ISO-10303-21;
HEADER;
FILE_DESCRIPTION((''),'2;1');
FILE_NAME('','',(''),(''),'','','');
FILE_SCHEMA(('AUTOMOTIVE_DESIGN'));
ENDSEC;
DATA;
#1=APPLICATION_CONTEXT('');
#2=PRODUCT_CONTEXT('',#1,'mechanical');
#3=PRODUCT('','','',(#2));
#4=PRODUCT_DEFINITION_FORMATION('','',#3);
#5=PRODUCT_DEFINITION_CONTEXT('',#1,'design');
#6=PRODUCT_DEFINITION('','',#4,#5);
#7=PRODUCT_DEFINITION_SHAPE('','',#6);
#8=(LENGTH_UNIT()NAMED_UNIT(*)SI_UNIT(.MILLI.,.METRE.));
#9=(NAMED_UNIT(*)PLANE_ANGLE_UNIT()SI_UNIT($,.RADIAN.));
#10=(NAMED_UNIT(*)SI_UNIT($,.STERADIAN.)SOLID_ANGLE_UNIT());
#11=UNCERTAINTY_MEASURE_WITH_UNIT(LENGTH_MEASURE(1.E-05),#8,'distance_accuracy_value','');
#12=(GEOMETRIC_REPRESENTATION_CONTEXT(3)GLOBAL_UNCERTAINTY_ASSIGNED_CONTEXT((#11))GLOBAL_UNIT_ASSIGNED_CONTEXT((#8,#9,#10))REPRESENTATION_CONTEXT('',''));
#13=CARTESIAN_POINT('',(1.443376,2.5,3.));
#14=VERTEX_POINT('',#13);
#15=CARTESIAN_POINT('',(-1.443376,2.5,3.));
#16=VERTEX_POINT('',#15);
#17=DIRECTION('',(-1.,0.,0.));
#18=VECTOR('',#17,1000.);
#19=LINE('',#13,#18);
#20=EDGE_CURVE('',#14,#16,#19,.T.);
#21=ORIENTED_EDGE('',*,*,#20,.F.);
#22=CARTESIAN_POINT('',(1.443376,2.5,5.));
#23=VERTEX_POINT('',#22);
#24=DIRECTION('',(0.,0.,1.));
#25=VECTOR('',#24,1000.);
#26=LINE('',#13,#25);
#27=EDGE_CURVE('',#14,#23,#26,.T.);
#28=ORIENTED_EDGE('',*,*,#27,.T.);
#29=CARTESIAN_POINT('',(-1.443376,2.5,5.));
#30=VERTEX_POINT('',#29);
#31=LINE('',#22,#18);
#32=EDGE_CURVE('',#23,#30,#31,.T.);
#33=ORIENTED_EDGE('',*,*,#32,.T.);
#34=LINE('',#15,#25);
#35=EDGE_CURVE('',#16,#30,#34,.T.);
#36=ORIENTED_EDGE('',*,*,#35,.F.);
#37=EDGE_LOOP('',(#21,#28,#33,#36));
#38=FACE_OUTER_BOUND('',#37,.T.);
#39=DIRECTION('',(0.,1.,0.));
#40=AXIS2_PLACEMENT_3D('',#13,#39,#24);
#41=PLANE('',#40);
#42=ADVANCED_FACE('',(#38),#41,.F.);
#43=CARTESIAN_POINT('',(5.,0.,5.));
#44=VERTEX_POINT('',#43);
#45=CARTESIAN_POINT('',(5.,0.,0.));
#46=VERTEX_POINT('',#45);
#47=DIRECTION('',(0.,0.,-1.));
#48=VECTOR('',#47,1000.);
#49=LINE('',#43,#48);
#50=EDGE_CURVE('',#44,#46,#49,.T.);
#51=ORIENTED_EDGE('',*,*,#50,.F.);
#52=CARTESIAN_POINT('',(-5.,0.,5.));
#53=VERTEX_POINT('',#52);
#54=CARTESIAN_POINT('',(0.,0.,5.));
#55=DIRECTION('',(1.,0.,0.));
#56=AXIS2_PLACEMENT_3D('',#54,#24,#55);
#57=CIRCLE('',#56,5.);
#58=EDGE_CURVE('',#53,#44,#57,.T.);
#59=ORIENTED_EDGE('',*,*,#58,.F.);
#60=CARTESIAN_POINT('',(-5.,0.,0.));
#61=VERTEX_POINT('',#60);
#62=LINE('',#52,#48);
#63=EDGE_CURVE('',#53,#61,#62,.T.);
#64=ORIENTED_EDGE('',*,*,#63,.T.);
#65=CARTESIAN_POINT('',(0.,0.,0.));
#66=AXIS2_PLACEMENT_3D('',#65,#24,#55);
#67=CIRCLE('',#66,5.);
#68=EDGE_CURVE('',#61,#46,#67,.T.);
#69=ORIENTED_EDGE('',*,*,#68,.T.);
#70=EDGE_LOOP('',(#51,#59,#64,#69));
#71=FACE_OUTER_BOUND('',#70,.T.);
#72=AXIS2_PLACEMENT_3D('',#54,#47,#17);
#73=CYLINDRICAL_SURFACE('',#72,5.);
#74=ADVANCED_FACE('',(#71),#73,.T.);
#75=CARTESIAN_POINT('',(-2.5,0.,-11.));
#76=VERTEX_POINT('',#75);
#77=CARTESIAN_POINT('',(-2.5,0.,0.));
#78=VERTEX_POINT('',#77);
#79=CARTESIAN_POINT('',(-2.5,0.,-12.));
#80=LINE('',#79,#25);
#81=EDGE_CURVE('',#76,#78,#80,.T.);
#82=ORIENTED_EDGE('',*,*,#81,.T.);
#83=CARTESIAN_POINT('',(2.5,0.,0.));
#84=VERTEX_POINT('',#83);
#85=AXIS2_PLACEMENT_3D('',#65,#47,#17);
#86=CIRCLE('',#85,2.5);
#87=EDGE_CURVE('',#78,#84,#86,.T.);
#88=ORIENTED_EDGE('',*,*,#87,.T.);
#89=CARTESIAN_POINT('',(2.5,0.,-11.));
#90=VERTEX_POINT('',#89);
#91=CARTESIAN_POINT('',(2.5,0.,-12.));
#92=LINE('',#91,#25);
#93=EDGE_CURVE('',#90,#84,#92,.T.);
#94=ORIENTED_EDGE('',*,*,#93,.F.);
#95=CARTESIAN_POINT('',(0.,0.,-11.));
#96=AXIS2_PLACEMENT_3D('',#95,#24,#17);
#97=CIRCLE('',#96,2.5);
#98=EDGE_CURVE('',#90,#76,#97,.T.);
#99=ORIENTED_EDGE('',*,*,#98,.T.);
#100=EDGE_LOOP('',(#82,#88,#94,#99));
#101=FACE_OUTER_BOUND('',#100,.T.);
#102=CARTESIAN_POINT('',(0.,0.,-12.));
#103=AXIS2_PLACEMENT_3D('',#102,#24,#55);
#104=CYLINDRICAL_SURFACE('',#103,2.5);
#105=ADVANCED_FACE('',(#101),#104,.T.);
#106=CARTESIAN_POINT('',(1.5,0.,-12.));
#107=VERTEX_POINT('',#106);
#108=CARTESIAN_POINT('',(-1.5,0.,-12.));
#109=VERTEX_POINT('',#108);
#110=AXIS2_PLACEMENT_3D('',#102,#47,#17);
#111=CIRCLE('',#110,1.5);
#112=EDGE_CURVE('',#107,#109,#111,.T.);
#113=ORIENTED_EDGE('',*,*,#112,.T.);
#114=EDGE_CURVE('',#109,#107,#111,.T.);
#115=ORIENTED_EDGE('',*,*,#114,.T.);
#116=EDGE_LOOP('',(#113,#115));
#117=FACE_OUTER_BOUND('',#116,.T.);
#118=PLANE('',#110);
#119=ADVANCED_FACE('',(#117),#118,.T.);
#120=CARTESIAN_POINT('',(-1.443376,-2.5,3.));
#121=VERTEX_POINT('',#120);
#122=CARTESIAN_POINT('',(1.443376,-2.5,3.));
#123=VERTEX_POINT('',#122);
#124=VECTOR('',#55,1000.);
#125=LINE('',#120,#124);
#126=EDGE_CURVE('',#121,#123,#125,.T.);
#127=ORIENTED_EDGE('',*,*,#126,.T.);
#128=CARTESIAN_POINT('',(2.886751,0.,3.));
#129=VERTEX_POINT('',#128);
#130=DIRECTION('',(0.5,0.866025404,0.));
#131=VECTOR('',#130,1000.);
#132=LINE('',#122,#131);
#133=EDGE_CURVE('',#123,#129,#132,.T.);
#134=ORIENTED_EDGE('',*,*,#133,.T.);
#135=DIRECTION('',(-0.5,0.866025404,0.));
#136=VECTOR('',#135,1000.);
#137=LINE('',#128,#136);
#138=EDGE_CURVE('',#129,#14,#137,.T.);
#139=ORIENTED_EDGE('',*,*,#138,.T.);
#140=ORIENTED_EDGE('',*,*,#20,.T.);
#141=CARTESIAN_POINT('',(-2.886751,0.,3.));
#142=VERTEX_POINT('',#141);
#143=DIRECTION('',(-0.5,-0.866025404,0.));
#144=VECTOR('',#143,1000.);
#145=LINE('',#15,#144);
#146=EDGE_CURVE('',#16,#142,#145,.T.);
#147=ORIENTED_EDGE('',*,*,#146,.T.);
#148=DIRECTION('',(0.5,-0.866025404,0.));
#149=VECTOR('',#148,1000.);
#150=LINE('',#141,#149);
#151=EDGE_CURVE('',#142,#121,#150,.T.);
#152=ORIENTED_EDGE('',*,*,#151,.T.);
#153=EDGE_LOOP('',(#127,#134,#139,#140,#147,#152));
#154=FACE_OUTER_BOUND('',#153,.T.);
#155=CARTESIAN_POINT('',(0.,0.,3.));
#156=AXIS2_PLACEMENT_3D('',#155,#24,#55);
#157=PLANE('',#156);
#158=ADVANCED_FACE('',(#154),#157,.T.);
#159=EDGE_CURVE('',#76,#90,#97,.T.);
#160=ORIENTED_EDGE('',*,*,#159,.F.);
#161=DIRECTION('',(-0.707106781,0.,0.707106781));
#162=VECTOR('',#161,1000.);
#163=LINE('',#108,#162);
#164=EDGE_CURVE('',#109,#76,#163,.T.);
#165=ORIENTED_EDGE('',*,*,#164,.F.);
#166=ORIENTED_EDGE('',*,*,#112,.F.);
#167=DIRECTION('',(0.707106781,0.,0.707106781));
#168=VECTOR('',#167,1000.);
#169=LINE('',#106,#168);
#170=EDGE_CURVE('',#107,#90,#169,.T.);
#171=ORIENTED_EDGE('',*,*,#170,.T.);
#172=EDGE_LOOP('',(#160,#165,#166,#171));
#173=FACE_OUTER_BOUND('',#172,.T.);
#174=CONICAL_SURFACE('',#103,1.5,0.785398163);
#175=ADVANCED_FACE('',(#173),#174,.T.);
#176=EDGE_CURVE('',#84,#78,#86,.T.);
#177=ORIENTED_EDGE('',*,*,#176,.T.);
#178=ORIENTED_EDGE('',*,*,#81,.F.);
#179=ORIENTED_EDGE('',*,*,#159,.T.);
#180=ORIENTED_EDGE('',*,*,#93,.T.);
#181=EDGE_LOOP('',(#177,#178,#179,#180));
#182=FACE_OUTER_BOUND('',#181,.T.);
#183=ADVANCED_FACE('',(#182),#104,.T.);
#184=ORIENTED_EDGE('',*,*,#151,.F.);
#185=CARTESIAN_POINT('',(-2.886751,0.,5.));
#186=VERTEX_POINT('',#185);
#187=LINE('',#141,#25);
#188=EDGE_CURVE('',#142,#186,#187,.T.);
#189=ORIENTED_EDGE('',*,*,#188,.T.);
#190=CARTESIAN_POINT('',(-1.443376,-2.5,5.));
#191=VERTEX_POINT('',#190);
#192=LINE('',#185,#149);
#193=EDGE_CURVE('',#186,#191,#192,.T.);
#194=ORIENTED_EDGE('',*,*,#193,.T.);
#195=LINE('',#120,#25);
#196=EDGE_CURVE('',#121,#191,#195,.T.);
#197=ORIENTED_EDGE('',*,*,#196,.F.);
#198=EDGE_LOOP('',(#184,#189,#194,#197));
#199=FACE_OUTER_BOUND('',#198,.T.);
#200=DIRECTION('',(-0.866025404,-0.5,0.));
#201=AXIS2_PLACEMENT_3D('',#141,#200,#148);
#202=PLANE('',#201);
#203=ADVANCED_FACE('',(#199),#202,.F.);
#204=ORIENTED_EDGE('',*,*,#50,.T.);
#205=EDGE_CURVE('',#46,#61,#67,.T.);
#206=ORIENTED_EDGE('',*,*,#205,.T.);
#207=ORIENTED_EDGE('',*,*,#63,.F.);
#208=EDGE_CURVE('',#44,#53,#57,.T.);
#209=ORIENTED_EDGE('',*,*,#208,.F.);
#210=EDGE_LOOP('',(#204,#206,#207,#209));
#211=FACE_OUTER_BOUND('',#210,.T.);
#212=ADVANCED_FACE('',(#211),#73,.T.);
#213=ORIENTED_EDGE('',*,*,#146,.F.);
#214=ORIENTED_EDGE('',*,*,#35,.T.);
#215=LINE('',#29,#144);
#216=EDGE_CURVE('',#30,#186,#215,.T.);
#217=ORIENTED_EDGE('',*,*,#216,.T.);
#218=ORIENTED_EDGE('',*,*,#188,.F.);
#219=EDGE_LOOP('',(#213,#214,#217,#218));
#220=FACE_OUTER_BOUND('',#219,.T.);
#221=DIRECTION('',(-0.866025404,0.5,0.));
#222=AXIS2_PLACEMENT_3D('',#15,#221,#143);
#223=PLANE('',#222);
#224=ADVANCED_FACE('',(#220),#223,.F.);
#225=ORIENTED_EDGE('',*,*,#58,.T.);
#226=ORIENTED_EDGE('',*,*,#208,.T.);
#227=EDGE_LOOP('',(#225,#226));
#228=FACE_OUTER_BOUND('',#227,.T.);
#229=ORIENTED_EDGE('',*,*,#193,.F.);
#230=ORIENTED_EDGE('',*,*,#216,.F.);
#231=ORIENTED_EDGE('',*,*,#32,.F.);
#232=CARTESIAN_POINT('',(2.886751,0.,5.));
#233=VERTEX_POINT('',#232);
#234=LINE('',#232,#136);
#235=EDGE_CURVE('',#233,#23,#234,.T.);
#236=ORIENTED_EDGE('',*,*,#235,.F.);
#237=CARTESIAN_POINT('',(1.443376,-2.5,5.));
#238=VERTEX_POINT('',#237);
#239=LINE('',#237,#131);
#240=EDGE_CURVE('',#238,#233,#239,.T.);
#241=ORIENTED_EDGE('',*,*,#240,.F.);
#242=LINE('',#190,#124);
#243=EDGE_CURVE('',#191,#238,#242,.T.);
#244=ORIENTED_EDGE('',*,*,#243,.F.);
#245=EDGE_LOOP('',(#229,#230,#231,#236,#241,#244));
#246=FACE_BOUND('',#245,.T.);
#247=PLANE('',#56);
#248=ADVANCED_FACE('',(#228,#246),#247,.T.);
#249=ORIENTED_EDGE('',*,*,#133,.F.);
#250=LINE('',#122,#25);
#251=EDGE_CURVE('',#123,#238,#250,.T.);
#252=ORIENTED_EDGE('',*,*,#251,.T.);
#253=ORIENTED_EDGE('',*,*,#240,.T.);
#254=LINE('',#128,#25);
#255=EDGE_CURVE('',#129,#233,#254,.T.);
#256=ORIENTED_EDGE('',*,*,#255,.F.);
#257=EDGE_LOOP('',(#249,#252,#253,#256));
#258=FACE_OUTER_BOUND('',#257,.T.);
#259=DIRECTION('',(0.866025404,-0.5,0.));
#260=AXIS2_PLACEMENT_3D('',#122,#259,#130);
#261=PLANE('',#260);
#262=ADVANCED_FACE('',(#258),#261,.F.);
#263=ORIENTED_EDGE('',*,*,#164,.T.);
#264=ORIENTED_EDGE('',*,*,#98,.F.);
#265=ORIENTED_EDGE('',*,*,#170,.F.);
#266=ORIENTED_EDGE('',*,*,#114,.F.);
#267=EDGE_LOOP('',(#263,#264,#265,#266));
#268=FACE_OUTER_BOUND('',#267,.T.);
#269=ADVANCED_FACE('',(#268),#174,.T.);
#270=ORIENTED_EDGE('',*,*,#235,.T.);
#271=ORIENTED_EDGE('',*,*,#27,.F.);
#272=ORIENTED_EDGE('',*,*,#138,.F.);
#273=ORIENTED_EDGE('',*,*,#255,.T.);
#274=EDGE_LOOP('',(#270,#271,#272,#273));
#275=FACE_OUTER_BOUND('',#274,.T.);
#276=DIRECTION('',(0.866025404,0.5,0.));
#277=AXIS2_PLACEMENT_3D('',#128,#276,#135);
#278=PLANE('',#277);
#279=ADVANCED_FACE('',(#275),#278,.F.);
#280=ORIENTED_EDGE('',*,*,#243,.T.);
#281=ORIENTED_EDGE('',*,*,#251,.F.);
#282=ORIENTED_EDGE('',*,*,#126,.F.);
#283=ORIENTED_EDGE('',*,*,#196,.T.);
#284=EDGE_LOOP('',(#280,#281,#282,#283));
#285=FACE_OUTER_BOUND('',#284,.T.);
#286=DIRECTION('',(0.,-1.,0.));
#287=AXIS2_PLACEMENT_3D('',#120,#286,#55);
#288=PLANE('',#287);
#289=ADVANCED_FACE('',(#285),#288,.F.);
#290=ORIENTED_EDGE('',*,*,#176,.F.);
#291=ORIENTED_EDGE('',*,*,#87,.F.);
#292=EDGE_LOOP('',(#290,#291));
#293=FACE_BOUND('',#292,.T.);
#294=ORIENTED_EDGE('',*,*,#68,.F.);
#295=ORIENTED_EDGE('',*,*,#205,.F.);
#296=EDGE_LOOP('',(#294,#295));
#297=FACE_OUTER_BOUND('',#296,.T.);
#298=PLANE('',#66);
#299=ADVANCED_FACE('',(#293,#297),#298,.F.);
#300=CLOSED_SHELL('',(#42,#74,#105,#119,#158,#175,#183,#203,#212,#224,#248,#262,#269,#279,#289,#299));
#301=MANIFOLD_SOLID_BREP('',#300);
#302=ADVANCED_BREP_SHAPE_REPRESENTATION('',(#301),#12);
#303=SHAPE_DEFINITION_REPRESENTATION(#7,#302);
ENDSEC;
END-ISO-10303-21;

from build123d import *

# Parameters (mm, degrees)
SKETCH1_R           = 5
BOSS_EXTRUDE1_DEPTH = 5
CUT_EXTRUDE1_DEPTH  = 2
SKETCH3_R           = 2.5
BOSS_EXTRUDE2_DEPTH = 12
CHAMFER1_SIZE       = 1


with BuildPart() as part:
    # Sketch1 → Boss-Extrude1 (new body)
    with BuildSketch(Plane.XY):
        Circle(SKETCH1_R)
    extrude(amount=BOSS_EXTRUDE1_DEPTH)

    # Sketch2 → Cut-Extrude1 (cut)
    with BuildSketch(Plane.XY.offset(5)):
        Polygon((2.886751346, 0), (1.443375673, 2.5), (-1.443375673, 2.5), (-2.886751346, 0), (-1.443375673, -2.5), (1.443375673, -2.5), align=None)
    extrude(amount=-CUT_EXTRUDE1_DEPTH, mode=Mode.SUBTRACT)

    # Sketch3 → Boss-Extrude2 (add)
    with BuildSketch(Plane(origin=(0, 0, 0), x_dir=(-1, 0, 0), z_dir=(0, 0, -1))):
        Circle(SKETCH3_R)
    extrude(amount=BOSS_EXTRUDE2_DEPTH)

    # Chamfer1
    chamfer1_edges = [part.edges().sort_by_distance(p)[0] for p in [
        (2.5, 0, -12),
    ]]
    chamfer(chamfer1_edges, length=CHAMFER1_SIZE)


solid = part.part
